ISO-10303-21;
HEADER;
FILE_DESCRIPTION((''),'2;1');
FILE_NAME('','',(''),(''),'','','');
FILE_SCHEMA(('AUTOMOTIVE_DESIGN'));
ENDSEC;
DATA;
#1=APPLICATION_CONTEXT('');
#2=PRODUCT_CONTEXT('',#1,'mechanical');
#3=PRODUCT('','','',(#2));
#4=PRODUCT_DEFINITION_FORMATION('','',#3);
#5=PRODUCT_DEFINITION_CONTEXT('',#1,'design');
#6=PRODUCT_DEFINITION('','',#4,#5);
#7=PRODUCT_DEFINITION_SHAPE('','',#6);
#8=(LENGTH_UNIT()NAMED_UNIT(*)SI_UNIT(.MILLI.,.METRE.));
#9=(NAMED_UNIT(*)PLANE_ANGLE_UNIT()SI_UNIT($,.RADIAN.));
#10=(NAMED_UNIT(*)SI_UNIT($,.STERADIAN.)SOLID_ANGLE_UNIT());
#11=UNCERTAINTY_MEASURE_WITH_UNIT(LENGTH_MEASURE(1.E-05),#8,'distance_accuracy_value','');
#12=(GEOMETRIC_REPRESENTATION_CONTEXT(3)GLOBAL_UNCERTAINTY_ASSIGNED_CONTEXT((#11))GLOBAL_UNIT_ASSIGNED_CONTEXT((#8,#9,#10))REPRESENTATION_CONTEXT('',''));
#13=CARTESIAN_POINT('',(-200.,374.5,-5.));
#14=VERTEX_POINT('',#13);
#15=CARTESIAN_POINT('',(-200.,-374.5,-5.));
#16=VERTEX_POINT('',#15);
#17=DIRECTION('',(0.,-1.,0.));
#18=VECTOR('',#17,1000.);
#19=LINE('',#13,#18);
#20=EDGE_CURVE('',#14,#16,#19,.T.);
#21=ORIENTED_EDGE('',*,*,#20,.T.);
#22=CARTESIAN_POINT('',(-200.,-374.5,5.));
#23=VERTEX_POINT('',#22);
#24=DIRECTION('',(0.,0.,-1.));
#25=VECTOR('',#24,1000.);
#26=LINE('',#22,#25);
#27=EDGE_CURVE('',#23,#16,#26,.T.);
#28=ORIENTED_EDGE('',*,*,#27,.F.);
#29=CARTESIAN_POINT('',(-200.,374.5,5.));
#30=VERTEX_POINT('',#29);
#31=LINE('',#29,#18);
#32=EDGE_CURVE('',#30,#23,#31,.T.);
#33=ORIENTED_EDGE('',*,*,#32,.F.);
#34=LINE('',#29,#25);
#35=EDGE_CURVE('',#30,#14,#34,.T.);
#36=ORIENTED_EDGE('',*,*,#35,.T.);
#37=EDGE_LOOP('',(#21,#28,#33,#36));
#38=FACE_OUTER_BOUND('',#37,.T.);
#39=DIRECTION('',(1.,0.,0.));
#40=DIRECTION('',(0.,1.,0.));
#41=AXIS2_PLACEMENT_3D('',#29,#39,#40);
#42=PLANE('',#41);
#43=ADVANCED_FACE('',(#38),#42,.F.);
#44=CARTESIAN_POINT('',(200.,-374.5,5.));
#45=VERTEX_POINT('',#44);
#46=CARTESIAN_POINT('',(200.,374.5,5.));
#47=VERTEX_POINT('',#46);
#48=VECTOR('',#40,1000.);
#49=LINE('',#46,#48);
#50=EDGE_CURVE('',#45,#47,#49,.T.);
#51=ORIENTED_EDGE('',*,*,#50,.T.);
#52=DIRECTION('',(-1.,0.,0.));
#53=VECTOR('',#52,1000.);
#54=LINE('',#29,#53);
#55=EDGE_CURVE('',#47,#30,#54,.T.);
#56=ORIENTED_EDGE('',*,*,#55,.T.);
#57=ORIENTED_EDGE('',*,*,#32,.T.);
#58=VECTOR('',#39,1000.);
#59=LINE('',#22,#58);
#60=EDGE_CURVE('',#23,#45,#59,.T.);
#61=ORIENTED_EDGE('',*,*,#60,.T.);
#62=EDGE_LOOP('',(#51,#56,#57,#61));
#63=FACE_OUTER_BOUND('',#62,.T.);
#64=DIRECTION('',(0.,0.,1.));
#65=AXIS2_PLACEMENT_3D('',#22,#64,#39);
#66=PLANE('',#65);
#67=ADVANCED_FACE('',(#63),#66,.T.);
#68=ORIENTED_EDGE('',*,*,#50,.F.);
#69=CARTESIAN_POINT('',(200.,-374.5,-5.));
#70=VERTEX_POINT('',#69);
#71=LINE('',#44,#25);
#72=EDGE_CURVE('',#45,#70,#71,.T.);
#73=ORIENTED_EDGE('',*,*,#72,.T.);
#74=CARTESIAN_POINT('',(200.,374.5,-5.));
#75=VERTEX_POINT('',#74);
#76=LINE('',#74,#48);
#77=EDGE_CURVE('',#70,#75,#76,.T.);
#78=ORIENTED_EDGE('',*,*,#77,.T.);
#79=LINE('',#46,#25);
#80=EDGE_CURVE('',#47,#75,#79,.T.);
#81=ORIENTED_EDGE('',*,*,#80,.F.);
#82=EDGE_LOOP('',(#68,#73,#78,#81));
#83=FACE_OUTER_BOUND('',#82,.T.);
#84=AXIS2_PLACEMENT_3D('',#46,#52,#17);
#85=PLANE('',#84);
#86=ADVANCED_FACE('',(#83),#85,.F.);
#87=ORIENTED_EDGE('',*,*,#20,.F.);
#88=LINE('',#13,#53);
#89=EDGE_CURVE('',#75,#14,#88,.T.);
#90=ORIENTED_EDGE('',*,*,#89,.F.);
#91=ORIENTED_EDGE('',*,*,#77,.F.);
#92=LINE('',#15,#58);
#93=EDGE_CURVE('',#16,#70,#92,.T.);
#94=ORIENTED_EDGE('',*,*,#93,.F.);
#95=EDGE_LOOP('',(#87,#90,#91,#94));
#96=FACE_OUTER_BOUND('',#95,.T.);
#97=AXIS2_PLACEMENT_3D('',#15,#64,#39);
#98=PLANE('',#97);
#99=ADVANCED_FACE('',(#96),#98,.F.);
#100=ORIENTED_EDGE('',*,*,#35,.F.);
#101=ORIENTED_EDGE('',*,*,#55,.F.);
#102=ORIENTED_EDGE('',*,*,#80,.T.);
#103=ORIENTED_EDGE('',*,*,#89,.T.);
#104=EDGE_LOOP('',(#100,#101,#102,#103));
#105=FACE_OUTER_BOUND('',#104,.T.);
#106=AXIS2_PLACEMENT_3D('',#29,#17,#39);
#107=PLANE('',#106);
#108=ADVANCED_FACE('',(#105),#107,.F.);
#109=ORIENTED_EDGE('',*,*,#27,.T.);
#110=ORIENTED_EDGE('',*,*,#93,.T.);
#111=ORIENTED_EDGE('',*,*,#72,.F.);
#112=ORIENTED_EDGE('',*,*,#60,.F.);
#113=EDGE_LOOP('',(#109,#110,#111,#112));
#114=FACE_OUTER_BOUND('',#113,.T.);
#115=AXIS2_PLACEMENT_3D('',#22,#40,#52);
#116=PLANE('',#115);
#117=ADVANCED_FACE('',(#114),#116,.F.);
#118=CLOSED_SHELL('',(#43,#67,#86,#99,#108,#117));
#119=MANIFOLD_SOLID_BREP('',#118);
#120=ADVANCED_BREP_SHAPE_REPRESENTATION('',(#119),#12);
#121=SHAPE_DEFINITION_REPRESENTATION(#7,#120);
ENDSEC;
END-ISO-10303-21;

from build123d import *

# Parameters (mm, degrees)
SKETCH1_W           = 400
SKETCH1_H           = 749
BOSS_EXTRUDE1_DEPTH = 5


with BuildPart() as part:
    # Sketch1 → Boss-Extrude1 (new, symmetric)
    with BuildSketch(Plane.XY):
        Rectangle(SKETCH1_W, SKETCH1_H)
    extrude(amount=BOSS_EXTRUDE1_DEPTH, both=True)


solid = part.part
